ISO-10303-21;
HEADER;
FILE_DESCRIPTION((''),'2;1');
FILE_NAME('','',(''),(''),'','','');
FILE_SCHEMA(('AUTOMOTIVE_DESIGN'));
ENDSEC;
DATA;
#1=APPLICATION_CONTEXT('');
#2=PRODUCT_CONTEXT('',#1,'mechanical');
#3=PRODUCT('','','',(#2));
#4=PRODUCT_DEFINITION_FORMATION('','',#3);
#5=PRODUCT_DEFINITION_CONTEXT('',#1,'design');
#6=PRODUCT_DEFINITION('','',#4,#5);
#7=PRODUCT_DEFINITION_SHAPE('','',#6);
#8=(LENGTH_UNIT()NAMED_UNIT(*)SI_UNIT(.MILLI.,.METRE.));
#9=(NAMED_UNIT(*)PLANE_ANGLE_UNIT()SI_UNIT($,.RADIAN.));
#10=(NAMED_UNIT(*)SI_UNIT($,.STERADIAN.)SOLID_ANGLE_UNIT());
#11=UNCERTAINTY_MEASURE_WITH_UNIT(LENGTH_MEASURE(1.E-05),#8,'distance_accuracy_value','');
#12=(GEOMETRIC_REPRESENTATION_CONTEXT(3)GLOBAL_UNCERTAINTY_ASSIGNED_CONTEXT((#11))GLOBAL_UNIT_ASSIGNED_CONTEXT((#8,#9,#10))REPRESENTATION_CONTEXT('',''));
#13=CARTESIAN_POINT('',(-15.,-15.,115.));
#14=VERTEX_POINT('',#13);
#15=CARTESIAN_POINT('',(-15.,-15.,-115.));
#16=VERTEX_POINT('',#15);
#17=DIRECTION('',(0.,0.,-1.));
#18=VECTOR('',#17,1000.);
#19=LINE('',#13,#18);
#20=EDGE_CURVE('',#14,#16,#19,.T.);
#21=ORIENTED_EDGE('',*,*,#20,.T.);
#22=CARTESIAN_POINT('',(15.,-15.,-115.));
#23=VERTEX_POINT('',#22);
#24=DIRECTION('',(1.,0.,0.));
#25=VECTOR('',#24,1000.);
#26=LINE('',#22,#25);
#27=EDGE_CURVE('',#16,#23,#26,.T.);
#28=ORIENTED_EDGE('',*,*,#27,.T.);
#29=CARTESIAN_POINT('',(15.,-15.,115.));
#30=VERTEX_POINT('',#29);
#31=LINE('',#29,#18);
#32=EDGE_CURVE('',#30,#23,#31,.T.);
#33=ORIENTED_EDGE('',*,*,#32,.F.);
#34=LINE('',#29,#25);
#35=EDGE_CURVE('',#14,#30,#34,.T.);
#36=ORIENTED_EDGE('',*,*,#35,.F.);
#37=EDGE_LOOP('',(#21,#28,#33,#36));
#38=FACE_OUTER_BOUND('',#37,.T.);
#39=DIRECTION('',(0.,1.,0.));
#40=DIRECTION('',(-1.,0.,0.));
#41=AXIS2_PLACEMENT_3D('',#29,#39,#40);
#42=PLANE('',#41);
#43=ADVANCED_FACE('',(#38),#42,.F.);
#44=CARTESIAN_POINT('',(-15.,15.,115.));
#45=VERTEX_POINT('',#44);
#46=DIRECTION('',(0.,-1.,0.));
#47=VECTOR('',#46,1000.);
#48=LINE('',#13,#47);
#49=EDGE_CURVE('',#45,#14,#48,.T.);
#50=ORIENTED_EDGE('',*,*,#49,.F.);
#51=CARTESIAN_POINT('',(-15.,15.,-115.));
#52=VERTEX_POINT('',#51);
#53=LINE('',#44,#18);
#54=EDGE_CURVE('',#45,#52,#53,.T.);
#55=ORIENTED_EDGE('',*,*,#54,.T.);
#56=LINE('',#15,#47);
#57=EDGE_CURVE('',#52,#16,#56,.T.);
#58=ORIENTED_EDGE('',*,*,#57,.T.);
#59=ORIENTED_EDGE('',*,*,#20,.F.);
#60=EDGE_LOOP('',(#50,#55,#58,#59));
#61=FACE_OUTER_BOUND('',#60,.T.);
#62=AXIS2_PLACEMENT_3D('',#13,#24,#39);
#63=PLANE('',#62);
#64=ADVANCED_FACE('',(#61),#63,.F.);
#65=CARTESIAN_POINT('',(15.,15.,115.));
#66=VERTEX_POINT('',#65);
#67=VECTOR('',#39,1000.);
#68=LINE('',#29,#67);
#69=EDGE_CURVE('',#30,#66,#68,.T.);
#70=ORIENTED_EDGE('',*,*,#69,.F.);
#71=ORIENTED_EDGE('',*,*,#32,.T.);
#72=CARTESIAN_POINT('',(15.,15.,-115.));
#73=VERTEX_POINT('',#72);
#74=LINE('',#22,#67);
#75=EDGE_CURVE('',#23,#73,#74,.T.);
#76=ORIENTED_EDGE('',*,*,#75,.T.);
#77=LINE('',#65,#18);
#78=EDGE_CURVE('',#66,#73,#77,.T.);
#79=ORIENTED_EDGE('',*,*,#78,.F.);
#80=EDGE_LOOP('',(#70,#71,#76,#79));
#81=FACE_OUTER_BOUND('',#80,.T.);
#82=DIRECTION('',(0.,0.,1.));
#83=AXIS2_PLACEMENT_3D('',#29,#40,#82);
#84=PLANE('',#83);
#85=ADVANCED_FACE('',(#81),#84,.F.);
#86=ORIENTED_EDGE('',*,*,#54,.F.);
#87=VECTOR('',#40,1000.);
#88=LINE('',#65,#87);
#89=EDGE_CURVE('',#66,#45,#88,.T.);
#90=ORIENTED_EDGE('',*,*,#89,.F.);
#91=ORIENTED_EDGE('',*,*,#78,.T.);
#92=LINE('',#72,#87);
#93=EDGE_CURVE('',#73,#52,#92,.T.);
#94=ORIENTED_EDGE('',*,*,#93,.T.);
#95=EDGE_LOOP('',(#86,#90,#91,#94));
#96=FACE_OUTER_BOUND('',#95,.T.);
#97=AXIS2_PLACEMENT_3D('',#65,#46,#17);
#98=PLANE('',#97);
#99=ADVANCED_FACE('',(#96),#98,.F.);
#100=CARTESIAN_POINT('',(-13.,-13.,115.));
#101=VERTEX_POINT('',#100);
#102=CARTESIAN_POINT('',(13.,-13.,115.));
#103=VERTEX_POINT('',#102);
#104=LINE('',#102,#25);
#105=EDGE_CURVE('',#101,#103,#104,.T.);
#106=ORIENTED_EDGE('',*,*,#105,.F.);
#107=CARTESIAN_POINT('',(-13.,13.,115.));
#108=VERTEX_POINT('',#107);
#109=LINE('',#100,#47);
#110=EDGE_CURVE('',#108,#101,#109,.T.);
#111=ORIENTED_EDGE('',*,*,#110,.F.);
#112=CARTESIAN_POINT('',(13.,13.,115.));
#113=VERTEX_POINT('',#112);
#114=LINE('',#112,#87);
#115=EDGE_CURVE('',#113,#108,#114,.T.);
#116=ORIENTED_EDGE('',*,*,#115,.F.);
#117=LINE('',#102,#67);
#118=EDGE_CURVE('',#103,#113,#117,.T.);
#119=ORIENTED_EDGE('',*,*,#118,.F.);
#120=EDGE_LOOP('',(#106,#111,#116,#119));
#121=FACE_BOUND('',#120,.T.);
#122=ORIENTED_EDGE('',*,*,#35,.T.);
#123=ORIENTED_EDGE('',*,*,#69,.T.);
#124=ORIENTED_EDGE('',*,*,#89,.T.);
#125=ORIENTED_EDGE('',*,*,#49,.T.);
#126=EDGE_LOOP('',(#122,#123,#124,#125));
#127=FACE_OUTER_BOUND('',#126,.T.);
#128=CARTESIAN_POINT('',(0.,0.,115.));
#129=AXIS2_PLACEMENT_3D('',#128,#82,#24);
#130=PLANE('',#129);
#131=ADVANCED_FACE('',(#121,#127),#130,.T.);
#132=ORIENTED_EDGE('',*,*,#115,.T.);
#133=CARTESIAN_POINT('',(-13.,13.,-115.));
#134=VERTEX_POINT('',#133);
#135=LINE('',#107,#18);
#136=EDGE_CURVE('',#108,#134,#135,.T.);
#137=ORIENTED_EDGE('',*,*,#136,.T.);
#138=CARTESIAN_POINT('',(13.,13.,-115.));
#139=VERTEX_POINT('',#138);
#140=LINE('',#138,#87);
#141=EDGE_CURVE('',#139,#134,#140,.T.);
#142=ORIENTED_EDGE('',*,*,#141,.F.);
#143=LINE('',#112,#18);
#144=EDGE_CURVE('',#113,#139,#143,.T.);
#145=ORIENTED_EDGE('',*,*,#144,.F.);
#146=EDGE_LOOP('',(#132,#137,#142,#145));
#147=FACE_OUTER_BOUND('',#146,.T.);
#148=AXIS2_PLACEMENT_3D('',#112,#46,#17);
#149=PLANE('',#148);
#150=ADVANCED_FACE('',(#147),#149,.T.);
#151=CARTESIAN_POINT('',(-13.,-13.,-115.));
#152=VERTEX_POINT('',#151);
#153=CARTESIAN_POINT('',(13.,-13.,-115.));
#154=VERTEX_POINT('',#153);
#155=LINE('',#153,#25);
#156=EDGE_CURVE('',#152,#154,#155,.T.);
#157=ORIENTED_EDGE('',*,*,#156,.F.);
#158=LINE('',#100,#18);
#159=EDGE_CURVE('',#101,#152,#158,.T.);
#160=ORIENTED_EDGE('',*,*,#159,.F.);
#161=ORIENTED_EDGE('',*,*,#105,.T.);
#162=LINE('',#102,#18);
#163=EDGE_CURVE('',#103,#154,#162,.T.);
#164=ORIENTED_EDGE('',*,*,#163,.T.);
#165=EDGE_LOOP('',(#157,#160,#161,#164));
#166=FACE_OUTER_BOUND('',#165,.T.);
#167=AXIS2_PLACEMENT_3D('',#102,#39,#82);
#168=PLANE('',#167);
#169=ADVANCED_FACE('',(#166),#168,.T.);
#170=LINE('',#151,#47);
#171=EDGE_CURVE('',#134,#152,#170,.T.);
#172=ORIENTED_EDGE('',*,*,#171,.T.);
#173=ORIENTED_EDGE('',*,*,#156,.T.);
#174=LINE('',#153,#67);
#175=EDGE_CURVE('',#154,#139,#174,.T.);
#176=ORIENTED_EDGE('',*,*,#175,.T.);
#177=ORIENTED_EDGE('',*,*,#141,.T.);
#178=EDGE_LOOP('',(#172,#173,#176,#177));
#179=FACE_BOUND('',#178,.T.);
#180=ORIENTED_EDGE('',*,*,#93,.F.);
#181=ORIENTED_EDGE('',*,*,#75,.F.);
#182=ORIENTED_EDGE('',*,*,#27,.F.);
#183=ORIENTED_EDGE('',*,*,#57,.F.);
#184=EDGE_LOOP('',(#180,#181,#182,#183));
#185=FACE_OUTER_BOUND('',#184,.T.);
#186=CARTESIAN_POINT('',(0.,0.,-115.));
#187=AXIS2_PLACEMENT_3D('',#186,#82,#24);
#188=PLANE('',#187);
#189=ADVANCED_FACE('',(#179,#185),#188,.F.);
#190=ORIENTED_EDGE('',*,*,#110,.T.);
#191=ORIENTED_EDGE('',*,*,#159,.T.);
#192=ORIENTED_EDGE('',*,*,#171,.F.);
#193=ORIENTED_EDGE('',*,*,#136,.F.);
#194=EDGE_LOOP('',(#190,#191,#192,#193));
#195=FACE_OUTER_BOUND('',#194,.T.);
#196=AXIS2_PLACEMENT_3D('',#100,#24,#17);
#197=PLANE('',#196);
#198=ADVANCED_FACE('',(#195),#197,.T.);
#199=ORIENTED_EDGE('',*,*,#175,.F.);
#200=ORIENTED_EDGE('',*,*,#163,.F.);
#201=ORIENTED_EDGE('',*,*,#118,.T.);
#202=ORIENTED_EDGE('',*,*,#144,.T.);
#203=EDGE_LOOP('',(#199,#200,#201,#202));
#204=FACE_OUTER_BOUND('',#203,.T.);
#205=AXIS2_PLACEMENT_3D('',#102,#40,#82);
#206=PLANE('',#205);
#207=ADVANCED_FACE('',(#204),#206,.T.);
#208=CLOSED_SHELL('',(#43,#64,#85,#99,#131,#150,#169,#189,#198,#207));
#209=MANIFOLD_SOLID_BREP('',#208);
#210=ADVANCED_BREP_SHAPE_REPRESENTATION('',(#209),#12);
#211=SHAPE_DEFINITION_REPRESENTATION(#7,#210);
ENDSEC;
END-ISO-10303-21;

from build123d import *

# Parameters (mm, degrees)
SKETCH_1_W      = 30
SKETCH_1_H      = 30
SKETCH_1_W_2    = 26
SKETCH_1_H_2    = 26
EXTRUDE_1_DEPTH = 115


with BuildPart() as part:
    # 草图1 → 凸台-拉伸1 (new, symmetric)
    with BuildSketch(Plane.XY):
        Rectangle(SKETCH_1_W, SKETCH_1_H)
        Rectangle(SKETCH_1_W_2, SKETCH_1_H_2, mode=Mode.SUBTRACT)
    extrude(amount=EXTRUDE_1_DEPTH, both=True)


solid = part.part
